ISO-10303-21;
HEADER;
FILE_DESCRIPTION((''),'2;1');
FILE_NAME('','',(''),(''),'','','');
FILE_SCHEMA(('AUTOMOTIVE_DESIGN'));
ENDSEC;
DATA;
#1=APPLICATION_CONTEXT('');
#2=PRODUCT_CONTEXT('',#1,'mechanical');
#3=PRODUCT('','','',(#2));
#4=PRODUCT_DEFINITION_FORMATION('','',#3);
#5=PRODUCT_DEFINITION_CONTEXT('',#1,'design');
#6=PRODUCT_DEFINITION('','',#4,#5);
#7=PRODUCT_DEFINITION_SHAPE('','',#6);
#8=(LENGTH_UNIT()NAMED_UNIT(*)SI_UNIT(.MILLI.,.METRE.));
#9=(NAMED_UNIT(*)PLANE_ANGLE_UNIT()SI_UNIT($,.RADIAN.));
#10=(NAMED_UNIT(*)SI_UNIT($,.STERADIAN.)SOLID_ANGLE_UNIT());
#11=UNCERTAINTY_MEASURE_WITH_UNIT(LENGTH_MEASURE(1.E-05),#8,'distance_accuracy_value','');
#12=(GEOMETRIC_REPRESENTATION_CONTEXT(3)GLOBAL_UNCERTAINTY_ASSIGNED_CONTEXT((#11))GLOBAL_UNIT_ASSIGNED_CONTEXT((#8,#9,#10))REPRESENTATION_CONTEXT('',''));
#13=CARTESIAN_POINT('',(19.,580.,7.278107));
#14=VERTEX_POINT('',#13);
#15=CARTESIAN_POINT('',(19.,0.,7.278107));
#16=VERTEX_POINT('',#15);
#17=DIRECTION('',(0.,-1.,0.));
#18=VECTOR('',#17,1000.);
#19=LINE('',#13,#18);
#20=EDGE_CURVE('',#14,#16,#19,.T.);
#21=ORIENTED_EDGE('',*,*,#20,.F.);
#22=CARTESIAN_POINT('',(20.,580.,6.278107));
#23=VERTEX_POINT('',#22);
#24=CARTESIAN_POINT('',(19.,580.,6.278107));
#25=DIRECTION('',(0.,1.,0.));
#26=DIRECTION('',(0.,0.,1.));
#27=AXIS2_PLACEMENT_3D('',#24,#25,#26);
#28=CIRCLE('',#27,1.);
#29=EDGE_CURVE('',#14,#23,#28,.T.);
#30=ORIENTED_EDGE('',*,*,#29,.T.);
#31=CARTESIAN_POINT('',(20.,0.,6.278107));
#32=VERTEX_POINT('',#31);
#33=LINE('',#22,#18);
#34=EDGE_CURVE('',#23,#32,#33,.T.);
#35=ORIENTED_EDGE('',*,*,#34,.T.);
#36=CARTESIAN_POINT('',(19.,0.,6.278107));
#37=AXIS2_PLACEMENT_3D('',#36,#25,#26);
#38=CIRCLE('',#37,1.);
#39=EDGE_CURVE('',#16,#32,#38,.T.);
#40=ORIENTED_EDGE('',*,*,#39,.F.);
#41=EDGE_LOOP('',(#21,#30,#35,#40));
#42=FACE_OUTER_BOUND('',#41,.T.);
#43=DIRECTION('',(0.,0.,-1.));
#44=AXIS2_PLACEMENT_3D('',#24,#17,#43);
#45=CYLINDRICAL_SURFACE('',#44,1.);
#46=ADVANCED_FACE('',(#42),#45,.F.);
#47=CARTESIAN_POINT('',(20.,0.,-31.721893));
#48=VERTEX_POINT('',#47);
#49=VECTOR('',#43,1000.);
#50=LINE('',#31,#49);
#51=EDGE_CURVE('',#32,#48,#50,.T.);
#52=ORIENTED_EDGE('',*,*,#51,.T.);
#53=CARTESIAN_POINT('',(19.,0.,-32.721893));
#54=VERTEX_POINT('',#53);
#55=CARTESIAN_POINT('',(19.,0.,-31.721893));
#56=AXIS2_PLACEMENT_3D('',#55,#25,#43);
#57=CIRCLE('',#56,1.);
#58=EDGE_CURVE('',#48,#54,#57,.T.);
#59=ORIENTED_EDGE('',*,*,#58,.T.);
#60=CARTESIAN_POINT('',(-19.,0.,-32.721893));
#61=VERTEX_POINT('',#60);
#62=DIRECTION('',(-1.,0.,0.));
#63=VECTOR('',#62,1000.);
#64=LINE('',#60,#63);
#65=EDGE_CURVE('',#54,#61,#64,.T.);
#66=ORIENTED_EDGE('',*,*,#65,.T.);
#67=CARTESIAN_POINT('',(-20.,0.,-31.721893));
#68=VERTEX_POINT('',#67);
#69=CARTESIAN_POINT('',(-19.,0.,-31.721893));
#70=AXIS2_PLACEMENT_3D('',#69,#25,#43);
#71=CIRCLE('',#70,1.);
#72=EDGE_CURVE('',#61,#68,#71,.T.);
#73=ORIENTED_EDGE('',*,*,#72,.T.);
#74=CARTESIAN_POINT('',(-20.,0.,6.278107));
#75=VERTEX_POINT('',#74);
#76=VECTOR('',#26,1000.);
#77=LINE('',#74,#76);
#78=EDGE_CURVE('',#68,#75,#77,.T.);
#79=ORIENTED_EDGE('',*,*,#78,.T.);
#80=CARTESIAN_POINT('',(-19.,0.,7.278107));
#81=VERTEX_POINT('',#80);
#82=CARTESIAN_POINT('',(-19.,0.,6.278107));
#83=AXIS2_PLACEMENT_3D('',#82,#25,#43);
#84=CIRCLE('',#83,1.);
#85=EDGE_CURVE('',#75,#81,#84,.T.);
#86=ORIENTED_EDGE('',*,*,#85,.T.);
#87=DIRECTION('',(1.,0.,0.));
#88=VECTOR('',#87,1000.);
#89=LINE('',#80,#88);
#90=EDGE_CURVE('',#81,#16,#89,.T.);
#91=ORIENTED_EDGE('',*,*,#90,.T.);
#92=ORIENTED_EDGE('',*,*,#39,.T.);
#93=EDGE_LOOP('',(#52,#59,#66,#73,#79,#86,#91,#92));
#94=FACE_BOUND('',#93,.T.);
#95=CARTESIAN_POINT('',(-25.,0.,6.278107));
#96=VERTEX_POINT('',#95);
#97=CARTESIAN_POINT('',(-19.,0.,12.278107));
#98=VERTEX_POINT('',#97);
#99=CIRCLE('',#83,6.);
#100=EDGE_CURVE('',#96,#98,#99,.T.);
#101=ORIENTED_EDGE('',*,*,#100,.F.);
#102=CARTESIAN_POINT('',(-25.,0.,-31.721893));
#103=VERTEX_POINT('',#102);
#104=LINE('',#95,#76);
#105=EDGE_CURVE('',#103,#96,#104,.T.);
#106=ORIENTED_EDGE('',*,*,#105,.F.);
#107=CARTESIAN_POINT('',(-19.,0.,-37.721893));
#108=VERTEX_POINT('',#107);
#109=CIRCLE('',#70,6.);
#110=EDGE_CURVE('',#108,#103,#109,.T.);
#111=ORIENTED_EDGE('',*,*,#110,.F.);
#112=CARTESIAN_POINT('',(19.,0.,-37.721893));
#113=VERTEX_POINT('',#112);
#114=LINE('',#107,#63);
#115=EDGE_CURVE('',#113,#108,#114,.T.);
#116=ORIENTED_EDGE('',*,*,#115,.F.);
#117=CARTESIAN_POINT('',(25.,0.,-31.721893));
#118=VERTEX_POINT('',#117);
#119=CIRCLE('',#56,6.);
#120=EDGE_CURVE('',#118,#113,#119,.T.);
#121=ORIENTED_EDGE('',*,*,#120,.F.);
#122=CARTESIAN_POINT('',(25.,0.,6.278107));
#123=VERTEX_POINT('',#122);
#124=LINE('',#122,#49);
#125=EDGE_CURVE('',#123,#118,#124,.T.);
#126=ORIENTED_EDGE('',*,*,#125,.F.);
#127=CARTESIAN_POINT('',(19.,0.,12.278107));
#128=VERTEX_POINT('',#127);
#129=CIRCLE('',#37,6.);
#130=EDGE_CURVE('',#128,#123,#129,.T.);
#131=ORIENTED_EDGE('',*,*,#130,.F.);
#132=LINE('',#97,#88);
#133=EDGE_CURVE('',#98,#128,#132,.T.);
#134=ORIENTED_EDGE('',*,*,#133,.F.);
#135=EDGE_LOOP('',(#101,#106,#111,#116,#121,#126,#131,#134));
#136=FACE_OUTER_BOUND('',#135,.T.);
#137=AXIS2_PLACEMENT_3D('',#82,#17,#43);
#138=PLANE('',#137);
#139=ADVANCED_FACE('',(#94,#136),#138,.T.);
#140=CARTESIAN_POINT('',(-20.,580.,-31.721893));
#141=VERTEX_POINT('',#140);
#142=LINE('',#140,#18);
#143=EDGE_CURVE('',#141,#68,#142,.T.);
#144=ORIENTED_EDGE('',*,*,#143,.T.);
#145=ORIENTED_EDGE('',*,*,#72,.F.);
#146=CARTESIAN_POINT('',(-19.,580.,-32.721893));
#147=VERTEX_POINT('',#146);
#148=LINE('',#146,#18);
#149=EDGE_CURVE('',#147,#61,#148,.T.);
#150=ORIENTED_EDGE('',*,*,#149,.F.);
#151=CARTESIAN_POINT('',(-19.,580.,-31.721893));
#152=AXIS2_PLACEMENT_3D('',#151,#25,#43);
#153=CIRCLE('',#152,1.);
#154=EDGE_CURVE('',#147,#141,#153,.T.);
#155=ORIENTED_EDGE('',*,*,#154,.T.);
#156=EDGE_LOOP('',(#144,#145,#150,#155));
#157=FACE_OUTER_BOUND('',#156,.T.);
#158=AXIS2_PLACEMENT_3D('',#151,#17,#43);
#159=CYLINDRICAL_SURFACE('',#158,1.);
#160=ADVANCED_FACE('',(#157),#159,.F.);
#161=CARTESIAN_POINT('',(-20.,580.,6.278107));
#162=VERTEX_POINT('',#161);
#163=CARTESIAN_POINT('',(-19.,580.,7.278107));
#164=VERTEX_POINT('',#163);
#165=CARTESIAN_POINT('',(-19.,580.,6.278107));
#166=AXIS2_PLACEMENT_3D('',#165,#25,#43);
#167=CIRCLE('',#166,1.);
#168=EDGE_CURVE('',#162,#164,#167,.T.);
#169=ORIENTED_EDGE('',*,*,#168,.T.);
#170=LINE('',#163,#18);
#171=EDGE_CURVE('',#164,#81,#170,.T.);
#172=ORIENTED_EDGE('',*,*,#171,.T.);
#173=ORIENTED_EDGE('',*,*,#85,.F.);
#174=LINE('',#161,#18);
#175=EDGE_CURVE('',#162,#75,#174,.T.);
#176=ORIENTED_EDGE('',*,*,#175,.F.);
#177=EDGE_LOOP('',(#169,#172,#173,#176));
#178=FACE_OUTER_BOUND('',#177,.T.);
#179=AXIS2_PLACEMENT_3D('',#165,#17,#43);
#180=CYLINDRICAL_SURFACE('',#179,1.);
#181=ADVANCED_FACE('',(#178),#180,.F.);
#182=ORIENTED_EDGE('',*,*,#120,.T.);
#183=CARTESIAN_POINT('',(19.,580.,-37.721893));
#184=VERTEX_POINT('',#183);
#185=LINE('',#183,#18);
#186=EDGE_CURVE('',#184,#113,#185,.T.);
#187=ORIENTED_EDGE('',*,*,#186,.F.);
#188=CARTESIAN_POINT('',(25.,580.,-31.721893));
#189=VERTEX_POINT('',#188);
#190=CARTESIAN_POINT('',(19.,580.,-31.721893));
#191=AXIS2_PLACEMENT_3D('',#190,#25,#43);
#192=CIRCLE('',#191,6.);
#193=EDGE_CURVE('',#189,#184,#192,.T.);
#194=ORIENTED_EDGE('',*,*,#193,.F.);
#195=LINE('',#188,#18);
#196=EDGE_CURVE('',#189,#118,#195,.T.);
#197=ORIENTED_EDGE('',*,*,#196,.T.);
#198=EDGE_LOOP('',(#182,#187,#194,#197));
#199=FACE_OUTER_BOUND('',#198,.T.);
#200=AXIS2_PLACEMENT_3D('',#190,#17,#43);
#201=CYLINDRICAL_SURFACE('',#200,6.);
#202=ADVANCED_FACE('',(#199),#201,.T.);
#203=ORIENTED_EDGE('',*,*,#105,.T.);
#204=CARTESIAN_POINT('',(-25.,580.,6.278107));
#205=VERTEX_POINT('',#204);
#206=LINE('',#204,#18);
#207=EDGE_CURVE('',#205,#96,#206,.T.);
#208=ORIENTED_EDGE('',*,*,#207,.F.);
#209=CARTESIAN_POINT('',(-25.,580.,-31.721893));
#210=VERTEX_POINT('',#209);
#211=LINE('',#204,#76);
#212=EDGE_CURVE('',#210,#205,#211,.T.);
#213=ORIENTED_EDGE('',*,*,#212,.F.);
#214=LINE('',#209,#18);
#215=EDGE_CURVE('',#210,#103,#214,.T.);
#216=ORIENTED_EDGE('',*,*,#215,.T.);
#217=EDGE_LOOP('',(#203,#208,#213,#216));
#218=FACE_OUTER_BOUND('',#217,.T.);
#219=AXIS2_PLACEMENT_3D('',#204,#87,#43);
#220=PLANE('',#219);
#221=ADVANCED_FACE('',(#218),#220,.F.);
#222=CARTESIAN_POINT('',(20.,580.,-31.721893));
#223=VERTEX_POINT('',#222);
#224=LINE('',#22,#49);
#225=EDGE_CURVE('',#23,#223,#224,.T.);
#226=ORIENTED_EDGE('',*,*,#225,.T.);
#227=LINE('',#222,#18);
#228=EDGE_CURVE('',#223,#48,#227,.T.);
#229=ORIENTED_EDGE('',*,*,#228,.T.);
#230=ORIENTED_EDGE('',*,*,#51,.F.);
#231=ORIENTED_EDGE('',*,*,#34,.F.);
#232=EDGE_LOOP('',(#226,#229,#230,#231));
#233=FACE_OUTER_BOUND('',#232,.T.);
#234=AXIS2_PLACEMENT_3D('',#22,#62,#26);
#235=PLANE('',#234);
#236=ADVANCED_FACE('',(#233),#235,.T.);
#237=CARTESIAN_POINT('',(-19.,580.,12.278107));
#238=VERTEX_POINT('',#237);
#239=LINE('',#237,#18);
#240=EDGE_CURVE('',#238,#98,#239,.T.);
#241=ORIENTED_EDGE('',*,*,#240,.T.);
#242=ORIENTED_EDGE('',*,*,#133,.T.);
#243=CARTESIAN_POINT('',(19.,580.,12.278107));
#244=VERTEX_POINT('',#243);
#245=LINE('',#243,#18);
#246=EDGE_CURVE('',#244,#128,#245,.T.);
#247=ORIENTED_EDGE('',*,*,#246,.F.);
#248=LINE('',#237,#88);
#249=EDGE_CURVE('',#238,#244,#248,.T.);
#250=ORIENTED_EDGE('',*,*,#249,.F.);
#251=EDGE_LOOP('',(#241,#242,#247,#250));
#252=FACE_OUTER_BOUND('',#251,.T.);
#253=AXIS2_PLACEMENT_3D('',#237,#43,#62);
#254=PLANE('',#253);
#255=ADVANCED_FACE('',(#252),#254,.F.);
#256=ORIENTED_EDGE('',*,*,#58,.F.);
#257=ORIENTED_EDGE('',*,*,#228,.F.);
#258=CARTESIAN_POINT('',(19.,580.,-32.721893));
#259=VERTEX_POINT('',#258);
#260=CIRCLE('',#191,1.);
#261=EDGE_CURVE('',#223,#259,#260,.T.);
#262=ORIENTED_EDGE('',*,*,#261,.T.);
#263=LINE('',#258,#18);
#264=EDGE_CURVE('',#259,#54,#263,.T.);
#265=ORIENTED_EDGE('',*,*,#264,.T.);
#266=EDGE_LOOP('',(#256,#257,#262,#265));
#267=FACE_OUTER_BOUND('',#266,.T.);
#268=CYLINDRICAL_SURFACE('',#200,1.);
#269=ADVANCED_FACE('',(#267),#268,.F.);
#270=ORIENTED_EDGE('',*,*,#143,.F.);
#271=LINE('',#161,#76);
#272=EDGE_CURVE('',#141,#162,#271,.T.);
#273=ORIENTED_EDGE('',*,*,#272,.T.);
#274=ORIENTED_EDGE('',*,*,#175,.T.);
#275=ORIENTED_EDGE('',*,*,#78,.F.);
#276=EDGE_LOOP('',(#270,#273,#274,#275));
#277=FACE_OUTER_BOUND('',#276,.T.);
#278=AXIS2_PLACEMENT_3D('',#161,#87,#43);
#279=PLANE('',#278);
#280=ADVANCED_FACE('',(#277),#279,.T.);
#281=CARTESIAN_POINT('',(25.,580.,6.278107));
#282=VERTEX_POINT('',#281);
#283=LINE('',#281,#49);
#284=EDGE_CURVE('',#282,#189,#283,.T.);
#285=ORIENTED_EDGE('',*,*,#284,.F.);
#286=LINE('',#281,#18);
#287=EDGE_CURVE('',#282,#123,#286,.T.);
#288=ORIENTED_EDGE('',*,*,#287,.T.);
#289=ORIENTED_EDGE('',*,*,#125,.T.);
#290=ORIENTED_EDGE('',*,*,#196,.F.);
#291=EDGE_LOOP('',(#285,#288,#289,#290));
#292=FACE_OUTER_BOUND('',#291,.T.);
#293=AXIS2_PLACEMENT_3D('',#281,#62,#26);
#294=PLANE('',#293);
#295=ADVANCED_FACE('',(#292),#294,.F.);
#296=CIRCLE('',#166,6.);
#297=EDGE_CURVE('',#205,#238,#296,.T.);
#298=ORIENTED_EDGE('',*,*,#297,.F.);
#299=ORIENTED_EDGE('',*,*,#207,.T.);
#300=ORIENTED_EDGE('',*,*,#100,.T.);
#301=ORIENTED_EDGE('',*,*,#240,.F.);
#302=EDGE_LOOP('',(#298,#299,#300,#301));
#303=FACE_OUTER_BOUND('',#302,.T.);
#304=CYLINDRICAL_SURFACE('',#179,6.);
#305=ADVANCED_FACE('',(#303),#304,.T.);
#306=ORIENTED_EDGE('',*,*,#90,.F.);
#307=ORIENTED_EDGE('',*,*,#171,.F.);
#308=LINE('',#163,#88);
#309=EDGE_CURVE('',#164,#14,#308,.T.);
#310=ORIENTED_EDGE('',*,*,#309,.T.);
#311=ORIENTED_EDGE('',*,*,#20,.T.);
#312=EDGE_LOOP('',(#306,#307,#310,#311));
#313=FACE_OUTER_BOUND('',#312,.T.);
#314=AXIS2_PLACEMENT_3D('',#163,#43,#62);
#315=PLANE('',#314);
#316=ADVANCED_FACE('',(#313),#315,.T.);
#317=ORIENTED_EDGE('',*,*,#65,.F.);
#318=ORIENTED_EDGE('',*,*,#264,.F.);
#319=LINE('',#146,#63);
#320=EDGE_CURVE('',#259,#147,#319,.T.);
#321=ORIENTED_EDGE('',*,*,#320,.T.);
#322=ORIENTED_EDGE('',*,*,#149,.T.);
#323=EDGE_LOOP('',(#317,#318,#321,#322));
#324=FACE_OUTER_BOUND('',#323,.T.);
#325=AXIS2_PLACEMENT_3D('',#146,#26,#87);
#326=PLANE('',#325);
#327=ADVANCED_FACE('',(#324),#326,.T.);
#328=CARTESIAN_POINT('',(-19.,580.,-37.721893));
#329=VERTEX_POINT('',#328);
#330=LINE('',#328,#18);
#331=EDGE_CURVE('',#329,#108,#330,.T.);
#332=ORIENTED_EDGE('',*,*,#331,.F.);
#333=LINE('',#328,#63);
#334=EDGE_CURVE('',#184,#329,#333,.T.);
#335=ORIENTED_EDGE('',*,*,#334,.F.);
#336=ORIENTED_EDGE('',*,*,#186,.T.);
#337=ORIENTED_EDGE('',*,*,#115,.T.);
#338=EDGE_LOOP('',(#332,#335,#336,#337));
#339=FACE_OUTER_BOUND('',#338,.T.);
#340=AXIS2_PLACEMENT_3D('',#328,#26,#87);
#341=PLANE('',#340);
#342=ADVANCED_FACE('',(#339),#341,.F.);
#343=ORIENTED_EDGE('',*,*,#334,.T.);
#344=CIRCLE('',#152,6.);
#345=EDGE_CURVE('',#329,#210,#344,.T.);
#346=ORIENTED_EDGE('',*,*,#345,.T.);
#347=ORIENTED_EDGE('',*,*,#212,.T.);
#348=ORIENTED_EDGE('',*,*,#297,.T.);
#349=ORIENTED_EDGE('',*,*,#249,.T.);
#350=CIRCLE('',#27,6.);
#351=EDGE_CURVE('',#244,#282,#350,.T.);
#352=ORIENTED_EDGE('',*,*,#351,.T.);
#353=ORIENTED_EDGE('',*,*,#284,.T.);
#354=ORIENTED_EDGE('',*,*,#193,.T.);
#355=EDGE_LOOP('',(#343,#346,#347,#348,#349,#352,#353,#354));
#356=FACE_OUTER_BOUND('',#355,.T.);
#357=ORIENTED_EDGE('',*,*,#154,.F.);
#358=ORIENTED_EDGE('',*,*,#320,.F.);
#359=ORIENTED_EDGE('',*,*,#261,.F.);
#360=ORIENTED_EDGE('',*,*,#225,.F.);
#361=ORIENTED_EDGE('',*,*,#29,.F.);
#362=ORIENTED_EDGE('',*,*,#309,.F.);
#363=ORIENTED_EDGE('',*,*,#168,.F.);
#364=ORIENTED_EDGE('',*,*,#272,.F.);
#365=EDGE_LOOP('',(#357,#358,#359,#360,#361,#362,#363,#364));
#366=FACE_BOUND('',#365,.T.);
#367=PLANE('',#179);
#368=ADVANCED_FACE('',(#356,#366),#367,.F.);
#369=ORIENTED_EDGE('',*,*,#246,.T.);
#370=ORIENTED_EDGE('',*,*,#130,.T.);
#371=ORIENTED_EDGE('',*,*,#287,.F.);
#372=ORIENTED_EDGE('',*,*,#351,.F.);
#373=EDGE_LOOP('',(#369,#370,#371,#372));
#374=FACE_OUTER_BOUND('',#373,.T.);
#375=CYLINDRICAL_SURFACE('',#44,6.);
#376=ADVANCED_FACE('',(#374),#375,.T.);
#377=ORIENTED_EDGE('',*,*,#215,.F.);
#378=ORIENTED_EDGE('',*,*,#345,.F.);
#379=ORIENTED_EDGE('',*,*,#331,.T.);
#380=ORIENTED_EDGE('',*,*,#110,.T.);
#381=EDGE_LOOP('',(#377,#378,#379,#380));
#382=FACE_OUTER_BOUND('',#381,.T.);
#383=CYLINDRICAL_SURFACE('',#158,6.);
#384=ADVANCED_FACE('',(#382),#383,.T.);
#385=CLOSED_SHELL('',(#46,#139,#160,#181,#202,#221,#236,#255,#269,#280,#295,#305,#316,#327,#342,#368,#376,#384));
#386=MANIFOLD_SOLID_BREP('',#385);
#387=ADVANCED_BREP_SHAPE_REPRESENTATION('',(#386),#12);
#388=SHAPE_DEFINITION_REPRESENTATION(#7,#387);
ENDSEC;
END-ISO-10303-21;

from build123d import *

# Parameters (mm, degrees)
EXTRUDE_1_DEPTH = 580


with BuildPart() as part:
    # 草图1 → 凸台-拉伸1 (new body)
    with BuildSketch(Plane(origin=(0, 0, 0), x_dir=(1, 0, 0), z_dir=(0, 1, 0))):
        with BuildLine():
            Line((-19, -12.278106509), (19, -12.278106509))
            ThreePointArc((19, -12.278106509), (23.242640687, -10.520747196), (25, -6.278106509))
            Line((25, -6.278106509), (25, 31.721893491))
            ThreePointArc((25, 31.721893491), (23.242640687, 35.964534178), (19, 37.721893491))
            Line((19, 37.721893491), (-19, 37.721893491))
            ThreePointArc((-19, 37.721893491), (-23.242640687, 35.964534178), (-25, 31.721893491))
            Line((-25, 31.721893491), (-25, -6.278106509))
            ThreePointArc((-25, -6.278106509), (-23.242640687, -10.520747196), (-19, -12.278106509))
        make_face()
        with BuildLine():
            Line((-19, -7.278106509), (19, -7.278106509))
            ThreePointArc((19, -7.278106509), (19.707106781, -6.98521329), (20, -6.278106509))
            Line((20, -6.278106509), (20, 31.721893491))
            ThreePointArc((20, 31.721893491), (19.707106781, 32.429000272), (19, 32.721893491))
            Line((19, 32.721893491), (-19, 32.721893491))
            ThreePointArc((-19, 32.721893491), (-19.707106781, 32.429000272), (-20, 31.721893491))
            Line((-20, 31.721893491), (-20, -6.278106509))
            ThreePointArc((-20, -6.278106509), (-19.707106781, -6.98521329), (-19, -7.278106509))
        make_face(mode=Mode.SUBTRACT)
    extrude(amount=EXTRUDE_1_DEPTH)


solid = part.part
